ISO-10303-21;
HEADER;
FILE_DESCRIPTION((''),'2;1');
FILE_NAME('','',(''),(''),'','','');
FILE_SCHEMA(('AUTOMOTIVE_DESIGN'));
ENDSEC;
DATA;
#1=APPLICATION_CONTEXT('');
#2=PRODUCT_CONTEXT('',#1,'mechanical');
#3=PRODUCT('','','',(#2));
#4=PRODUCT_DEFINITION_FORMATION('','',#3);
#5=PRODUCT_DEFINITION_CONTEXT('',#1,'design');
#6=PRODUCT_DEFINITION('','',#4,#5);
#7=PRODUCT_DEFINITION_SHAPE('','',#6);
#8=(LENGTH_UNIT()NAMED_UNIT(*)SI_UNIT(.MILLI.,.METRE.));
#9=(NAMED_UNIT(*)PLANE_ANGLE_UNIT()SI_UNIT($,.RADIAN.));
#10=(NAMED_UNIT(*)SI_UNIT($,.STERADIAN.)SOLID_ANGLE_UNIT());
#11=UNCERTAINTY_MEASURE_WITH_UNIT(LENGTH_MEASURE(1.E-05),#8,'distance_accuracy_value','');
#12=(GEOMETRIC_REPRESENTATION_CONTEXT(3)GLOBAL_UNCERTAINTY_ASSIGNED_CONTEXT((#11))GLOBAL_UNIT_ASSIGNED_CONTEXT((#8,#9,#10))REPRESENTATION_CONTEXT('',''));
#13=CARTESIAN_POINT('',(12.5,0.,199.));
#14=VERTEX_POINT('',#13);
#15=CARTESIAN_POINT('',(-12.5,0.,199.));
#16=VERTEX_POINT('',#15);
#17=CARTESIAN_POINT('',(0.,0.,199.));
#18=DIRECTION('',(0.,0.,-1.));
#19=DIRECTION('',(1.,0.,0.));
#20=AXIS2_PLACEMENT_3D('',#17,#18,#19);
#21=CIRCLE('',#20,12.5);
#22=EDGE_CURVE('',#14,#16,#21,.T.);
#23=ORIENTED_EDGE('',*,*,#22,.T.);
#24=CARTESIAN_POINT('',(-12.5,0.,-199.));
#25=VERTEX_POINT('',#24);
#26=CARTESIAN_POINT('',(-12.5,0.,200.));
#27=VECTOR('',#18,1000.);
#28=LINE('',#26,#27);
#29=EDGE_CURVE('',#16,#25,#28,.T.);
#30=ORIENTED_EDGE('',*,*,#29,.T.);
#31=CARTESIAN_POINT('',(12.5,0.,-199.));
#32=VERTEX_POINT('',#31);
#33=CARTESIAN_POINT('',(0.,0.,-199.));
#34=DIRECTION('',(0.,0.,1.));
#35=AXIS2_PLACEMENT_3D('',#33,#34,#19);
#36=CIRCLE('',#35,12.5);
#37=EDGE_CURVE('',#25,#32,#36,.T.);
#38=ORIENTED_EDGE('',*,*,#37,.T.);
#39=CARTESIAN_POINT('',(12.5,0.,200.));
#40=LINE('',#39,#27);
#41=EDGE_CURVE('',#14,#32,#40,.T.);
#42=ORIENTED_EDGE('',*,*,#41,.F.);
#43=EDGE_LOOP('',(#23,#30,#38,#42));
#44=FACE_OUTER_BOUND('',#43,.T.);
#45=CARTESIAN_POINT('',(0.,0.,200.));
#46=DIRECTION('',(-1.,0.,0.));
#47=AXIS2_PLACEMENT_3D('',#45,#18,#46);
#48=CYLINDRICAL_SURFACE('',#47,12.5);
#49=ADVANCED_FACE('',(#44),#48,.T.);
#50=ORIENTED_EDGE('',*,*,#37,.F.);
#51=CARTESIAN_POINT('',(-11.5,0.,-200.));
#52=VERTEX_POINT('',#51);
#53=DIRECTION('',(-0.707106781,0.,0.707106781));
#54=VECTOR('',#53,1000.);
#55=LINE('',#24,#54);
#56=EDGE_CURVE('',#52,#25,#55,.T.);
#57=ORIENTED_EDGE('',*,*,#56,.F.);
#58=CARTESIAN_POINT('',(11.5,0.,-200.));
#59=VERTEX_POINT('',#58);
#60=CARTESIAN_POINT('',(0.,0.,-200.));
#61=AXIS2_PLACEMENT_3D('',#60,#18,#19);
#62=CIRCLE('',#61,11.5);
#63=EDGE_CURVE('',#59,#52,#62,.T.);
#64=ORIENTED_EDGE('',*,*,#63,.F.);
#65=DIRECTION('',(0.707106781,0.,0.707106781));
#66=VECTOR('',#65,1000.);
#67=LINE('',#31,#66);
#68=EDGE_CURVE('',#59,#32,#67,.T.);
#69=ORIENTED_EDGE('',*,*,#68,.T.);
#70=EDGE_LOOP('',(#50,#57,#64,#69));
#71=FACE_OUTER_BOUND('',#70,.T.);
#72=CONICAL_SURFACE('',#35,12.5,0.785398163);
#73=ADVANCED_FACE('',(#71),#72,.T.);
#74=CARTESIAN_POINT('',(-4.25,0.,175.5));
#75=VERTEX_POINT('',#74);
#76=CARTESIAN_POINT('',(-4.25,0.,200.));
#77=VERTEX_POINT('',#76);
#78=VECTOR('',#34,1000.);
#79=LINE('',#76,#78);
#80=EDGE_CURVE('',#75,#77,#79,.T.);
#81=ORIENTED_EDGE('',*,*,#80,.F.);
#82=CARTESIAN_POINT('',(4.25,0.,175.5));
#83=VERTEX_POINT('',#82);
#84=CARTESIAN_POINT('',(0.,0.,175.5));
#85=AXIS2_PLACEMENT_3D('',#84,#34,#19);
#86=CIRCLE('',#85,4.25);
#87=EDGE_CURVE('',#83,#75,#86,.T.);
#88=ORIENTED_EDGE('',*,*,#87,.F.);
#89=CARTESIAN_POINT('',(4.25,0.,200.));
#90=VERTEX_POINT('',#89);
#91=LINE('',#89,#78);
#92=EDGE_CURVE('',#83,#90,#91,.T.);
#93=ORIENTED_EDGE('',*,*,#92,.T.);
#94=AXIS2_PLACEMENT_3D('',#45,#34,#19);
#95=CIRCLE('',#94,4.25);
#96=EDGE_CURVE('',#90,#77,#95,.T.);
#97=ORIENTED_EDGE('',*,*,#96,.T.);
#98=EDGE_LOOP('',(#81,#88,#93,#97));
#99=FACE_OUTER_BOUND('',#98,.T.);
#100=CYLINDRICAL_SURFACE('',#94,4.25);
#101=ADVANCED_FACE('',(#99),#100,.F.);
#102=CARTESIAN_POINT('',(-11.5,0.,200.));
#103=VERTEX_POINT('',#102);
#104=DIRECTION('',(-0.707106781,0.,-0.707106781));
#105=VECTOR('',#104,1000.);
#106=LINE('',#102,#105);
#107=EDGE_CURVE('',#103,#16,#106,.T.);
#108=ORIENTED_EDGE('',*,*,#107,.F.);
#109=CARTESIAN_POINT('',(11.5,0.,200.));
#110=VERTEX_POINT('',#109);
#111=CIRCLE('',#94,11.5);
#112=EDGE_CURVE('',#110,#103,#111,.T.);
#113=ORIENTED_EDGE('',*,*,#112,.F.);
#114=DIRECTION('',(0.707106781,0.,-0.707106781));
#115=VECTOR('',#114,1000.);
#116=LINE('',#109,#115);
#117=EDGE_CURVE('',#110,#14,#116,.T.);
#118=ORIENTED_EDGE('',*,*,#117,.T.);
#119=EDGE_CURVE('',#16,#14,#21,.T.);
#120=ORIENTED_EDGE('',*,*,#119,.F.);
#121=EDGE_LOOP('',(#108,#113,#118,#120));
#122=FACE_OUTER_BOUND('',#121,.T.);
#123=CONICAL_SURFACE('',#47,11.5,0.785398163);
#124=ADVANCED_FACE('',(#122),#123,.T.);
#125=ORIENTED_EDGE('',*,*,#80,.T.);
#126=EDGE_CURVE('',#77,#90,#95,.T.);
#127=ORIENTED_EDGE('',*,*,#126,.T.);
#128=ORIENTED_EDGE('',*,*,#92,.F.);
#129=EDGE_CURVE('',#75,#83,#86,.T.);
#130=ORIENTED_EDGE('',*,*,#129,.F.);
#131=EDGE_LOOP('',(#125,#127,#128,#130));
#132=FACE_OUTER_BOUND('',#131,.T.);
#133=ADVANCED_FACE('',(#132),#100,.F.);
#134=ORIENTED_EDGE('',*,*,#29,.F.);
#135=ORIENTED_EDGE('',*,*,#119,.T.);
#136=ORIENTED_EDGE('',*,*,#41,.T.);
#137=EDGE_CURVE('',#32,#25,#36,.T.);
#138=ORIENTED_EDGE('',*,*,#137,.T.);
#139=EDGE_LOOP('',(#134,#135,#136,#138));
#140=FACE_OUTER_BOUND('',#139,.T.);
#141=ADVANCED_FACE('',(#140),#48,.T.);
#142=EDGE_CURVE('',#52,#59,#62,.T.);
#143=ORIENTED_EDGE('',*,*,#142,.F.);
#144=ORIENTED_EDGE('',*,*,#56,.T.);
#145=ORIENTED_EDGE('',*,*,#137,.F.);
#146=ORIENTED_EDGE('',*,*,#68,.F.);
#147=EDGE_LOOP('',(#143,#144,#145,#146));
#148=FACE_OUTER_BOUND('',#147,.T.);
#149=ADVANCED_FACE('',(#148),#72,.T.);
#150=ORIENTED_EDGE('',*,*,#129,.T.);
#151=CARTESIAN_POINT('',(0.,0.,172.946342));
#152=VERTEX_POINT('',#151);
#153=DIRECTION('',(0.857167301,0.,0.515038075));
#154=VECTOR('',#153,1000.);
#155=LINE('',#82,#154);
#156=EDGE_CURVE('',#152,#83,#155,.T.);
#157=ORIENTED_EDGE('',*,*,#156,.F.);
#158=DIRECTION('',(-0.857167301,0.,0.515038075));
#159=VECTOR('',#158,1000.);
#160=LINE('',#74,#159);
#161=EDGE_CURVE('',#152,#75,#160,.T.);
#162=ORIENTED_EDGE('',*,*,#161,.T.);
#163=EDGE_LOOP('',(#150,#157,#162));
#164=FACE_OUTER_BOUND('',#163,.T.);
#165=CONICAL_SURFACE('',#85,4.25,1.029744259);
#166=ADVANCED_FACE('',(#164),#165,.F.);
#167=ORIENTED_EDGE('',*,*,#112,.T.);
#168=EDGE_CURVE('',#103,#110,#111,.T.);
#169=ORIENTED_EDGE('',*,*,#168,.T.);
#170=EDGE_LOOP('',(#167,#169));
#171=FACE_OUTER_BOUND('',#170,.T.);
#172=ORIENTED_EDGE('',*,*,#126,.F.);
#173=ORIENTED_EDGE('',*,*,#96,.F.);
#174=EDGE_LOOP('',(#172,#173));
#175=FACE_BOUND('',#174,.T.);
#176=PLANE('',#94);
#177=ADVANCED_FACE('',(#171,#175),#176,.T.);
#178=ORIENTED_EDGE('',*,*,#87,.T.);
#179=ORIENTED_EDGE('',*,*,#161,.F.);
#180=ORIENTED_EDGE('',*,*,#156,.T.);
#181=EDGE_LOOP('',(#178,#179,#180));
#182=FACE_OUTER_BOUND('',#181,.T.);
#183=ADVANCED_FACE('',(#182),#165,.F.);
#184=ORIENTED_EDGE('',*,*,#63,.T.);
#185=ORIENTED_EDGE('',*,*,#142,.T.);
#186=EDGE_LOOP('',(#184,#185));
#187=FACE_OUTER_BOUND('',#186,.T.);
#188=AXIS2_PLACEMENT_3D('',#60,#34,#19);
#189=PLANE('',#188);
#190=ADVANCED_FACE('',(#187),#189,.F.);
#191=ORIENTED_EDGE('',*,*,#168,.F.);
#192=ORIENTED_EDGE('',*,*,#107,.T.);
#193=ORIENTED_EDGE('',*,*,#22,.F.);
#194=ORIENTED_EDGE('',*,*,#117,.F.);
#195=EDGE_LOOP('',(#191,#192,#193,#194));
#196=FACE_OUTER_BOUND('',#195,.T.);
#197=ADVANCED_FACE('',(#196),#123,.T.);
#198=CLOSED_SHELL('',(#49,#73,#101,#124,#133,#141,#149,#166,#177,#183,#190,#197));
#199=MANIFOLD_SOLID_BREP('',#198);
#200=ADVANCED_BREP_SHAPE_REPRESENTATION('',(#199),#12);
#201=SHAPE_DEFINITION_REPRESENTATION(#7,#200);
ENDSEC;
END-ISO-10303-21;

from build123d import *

# Parameters (mm, degrees)
SKETCH_1_R              = 12.5
EXTRUDE_1_DEPTH         = 200
CHAMFER_1_SIZE          = 1
HOLE_WIZARD_M10_1_D     = 8.5
HOLE_WIZARD_M10_1_DEPTH = 24.5
HOLE_WIZARD_M10_1_TIP   = 2.553657631


with BuildPart() as part:
    # 草图1 → 凸台-拉伸1 (new, symmetric)
    with BuildSketch(Plane.XY):
        Circle(SKETCH_1_R)
    extrude(amount=EXTRUDE_1_DEPTH, both=True)

    # 倒角1
    chamfer_1_edges = [part.edges().sort_by_distance(p)[0] for p in [
        (-12.5, 0, -200),
        (-12.5, 0, 200),
    ]]
    chamfer(chamfer_1_edges, length=CHAMFER_1_SIZE)

    # M10 螺纹孔1
    with Locations(Plane.XY.offset(200)):
        with Locations((0, 0)):
            Hole(HOLE_WIZARD_M10_1_D / 2, depth=HOLE_WIZARD_M10_1_DEPTH)
            with Locations((0, 0, -(HOLE_WIZARD_M10_1_DEPTH + HOLE_WIZARD_M10_1_TIP / 2))):  # 118° drill point
                Cone(0, HOLE_WIZARD_M10_1_D / 2, HOLE_WIZARD_M10_1_TIP, mode=Mode.SUBTRACT)


solid = part.part
